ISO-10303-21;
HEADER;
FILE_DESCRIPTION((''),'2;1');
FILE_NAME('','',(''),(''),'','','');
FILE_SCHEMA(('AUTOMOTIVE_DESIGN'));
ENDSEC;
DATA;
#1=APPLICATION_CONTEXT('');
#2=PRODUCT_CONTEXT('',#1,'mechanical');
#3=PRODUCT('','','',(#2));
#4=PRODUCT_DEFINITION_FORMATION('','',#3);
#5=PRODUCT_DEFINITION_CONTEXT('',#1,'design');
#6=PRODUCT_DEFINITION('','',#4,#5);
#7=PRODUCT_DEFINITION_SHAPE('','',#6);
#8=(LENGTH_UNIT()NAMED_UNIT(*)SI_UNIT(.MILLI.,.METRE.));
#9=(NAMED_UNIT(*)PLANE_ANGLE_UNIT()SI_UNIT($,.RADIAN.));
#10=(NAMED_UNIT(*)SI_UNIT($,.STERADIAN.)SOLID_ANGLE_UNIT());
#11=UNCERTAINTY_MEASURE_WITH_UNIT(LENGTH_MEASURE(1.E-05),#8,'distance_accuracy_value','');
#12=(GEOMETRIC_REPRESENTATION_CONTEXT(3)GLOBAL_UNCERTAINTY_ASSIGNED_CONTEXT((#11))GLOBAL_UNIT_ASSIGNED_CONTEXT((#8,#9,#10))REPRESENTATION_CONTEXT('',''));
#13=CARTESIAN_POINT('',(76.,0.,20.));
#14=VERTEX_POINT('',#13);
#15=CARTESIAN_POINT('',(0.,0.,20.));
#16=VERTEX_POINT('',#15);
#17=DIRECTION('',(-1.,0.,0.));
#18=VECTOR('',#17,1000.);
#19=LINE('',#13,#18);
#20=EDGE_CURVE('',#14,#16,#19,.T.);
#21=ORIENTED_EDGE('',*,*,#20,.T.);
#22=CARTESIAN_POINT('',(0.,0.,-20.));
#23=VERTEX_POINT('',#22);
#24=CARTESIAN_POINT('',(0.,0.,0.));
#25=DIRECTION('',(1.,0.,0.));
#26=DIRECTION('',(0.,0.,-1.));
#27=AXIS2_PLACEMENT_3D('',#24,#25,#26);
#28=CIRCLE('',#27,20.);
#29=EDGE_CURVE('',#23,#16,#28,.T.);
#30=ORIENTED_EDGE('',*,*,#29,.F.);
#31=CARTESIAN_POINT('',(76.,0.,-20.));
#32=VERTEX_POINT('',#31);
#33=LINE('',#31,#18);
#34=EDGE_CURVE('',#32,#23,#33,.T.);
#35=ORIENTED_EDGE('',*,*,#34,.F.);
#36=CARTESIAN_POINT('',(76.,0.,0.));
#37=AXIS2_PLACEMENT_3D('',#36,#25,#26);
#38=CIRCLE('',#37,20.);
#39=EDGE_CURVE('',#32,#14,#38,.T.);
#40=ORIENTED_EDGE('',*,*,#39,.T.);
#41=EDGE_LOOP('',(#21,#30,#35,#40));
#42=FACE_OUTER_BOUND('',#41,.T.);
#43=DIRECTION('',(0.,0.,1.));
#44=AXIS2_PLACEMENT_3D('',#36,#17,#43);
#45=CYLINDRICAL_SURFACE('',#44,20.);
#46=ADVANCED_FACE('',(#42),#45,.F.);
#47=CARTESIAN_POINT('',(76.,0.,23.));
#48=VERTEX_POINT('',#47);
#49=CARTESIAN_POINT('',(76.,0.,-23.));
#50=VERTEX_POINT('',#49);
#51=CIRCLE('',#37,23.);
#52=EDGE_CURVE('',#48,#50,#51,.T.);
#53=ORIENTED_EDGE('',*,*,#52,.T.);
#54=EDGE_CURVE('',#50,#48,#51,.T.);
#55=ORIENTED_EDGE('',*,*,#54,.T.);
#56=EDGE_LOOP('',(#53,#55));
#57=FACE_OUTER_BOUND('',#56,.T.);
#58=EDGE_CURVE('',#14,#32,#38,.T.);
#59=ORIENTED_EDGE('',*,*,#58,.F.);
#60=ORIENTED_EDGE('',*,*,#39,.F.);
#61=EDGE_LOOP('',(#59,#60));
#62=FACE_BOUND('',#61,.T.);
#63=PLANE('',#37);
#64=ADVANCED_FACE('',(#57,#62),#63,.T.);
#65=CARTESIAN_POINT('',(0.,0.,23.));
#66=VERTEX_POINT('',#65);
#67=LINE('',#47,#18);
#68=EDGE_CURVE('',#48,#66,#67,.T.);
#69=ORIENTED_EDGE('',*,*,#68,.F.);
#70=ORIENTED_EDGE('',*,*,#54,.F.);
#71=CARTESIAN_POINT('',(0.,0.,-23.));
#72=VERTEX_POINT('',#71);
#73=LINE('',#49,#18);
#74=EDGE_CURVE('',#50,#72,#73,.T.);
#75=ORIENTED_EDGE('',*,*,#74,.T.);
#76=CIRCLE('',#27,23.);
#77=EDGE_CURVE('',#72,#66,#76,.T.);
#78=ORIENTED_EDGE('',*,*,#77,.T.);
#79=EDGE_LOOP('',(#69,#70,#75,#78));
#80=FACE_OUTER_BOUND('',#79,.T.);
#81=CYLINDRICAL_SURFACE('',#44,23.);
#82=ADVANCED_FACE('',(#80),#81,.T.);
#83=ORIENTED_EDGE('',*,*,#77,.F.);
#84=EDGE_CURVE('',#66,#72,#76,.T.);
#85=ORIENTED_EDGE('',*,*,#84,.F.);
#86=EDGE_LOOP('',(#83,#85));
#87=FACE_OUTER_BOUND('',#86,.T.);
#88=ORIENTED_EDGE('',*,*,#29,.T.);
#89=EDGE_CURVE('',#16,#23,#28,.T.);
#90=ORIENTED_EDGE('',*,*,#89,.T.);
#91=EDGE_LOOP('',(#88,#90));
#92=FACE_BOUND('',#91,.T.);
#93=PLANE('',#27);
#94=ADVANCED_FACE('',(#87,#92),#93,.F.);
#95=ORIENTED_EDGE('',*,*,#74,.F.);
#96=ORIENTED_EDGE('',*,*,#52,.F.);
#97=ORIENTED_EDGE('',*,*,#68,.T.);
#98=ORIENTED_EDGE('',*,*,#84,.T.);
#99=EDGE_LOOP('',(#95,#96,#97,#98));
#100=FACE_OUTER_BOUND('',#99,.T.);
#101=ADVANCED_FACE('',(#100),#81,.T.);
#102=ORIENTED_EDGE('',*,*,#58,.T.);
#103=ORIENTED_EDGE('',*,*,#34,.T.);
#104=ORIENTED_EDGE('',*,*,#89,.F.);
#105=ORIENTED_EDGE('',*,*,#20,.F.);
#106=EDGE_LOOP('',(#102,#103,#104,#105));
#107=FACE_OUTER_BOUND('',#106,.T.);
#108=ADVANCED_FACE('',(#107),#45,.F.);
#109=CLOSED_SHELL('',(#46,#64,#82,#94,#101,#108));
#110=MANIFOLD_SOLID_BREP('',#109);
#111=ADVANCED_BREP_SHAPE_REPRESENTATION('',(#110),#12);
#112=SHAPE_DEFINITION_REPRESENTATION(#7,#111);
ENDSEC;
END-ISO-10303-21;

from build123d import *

# Parameters (mm, degrees)
SKETCH_1_R      = 23
SKETCH_1_R_2    = 20
EXTRUDE_1_DEPTH = 76


with BuildPart() as part:
    # 草图1 → 凸台-拉伸1 (new body)
    with BuildSketch(Plane(origin=(0, 0, 0), x_dir=(0, 0, -1), z_dir=(1, 0, 0))):
        Circle(SKETCH_1_R)
        Circle(SKETCH_1_R_2, mode=Mode.SUBTRACT)
    extrude(amount=EXTRUDE_1_DEPTH)


solid = part.part
